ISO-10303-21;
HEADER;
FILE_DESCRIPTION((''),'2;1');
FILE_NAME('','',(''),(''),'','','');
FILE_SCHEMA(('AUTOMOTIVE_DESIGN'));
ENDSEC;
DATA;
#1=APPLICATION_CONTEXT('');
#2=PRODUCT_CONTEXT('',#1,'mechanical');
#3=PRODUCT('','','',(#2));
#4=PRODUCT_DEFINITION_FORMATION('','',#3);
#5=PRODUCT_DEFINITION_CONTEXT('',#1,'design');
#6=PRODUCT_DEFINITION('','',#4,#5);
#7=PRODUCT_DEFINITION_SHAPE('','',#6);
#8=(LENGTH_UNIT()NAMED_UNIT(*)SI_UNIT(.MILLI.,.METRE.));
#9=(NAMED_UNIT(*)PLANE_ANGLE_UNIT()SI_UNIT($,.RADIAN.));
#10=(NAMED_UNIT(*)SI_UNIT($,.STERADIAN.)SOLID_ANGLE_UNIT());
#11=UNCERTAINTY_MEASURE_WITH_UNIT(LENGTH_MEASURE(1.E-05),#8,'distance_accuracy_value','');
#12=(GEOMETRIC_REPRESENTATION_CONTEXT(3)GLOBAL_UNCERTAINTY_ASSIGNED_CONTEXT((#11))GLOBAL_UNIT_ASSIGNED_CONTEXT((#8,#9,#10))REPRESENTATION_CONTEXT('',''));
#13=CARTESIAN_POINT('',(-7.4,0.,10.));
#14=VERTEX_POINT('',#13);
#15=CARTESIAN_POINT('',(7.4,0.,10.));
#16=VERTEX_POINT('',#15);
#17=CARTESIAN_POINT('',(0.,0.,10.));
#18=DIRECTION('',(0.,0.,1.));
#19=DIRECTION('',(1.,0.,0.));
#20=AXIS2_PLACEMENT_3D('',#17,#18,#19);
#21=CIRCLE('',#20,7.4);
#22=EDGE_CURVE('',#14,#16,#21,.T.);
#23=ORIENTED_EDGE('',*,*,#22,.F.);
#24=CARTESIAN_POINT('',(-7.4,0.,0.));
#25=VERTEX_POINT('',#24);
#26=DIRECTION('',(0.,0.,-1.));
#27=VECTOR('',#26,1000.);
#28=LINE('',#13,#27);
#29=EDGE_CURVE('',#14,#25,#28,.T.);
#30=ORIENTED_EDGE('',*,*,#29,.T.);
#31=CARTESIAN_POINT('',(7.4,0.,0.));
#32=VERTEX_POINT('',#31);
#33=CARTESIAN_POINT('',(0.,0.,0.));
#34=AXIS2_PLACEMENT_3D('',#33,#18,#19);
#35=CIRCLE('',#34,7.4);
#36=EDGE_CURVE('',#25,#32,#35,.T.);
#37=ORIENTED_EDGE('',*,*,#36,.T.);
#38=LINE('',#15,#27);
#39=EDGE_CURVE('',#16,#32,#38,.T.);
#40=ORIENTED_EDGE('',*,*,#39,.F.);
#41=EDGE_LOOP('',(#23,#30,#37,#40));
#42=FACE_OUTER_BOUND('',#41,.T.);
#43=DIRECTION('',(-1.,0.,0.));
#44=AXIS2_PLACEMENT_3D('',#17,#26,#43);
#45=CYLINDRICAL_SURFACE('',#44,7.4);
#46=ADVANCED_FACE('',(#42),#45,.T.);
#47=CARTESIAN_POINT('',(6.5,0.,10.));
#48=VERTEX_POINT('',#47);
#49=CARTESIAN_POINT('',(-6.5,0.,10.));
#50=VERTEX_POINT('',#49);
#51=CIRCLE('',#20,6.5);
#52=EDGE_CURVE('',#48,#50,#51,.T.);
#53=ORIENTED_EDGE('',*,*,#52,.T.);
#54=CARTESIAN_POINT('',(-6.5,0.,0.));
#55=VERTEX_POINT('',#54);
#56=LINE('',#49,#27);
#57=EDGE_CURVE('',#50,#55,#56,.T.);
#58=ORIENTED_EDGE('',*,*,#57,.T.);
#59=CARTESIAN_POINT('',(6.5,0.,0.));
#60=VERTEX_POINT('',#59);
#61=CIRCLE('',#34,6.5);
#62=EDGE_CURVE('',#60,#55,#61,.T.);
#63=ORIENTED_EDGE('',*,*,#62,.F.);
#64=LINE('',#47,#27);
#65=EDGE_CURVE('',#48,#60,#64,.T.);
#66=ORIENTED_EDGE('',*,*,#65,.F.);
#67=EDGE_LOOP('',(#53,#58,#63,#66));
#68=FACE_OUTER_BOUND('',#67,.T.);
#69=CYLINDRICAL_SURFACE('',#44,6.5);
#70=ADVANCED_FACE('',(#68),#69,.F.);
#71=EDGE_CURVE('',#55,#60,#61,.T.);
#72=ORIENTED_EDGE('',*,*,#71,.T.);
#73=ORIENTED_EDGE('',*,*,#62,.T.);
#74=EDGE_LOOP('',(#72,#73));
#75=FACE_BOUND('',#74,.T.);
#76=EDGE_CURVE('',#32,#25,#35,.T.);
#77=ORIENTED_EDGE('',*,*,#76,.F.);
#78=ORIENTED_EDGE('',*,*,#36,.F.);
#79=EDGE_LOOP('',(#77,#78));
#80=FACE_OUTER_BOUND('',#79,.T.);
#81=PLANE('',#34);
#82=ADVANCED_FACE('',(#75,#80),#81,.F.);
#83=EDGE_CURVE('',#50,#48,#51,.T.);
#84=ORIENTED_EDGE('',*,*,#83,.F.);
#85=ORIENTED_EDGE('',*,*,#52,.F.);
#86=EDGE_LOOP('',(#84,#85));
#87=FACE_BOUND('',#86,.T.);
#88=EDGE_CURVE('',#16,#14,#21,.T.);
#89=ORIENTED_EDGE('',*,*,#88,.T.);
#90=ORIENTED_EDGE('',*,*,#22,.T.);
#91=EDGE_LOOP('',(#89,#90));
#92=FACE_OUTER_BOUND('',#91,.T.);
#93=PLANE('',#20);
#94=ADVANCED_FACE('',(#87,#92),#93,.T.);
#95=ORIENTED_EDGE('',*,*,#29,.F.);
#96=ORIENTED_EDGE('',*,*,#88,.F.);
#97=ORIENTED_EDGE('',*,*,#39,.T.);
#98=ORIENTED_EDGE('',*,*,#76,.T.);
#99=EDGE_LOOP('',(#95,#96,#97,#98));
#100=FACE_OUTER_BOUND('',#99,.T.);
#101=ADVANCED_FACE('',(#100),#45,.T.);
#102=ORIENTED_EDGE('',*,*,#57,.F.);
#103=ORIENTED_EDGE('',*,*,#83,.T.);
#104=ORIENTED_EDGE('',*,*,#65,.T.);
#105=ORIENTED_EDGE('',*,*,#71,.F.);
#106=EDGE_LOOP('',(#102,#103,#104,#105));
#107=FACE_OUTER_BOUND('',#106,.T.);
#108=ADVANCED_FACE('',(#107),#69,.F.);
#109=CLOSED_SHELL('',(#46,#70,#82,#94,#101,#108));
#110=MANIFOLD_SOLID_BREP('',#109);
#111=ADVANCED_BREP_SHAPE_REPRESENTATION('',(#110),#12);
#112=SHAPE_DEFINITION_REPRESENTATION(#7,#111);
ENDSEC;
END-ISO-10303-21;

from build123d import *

# Parameters (mm, degrees)
SKETCH_1_R      = 7.4
SKETCH_1_R_2    = 6.5
EXTRUDE_1_DEPTH = 10


with BuildPart() as part:
    # 草图1 → 凸台-拉伸1 (new body)
    with BuildSketch(Plane.XY):
        Circle(SKETCH_1_R)
        Circle(SKETCH_1_R_2, mode=Mode.SUBTRACT)
    extrude(amount=EXTRUDE_1_DEPTH)


solid = part.part
